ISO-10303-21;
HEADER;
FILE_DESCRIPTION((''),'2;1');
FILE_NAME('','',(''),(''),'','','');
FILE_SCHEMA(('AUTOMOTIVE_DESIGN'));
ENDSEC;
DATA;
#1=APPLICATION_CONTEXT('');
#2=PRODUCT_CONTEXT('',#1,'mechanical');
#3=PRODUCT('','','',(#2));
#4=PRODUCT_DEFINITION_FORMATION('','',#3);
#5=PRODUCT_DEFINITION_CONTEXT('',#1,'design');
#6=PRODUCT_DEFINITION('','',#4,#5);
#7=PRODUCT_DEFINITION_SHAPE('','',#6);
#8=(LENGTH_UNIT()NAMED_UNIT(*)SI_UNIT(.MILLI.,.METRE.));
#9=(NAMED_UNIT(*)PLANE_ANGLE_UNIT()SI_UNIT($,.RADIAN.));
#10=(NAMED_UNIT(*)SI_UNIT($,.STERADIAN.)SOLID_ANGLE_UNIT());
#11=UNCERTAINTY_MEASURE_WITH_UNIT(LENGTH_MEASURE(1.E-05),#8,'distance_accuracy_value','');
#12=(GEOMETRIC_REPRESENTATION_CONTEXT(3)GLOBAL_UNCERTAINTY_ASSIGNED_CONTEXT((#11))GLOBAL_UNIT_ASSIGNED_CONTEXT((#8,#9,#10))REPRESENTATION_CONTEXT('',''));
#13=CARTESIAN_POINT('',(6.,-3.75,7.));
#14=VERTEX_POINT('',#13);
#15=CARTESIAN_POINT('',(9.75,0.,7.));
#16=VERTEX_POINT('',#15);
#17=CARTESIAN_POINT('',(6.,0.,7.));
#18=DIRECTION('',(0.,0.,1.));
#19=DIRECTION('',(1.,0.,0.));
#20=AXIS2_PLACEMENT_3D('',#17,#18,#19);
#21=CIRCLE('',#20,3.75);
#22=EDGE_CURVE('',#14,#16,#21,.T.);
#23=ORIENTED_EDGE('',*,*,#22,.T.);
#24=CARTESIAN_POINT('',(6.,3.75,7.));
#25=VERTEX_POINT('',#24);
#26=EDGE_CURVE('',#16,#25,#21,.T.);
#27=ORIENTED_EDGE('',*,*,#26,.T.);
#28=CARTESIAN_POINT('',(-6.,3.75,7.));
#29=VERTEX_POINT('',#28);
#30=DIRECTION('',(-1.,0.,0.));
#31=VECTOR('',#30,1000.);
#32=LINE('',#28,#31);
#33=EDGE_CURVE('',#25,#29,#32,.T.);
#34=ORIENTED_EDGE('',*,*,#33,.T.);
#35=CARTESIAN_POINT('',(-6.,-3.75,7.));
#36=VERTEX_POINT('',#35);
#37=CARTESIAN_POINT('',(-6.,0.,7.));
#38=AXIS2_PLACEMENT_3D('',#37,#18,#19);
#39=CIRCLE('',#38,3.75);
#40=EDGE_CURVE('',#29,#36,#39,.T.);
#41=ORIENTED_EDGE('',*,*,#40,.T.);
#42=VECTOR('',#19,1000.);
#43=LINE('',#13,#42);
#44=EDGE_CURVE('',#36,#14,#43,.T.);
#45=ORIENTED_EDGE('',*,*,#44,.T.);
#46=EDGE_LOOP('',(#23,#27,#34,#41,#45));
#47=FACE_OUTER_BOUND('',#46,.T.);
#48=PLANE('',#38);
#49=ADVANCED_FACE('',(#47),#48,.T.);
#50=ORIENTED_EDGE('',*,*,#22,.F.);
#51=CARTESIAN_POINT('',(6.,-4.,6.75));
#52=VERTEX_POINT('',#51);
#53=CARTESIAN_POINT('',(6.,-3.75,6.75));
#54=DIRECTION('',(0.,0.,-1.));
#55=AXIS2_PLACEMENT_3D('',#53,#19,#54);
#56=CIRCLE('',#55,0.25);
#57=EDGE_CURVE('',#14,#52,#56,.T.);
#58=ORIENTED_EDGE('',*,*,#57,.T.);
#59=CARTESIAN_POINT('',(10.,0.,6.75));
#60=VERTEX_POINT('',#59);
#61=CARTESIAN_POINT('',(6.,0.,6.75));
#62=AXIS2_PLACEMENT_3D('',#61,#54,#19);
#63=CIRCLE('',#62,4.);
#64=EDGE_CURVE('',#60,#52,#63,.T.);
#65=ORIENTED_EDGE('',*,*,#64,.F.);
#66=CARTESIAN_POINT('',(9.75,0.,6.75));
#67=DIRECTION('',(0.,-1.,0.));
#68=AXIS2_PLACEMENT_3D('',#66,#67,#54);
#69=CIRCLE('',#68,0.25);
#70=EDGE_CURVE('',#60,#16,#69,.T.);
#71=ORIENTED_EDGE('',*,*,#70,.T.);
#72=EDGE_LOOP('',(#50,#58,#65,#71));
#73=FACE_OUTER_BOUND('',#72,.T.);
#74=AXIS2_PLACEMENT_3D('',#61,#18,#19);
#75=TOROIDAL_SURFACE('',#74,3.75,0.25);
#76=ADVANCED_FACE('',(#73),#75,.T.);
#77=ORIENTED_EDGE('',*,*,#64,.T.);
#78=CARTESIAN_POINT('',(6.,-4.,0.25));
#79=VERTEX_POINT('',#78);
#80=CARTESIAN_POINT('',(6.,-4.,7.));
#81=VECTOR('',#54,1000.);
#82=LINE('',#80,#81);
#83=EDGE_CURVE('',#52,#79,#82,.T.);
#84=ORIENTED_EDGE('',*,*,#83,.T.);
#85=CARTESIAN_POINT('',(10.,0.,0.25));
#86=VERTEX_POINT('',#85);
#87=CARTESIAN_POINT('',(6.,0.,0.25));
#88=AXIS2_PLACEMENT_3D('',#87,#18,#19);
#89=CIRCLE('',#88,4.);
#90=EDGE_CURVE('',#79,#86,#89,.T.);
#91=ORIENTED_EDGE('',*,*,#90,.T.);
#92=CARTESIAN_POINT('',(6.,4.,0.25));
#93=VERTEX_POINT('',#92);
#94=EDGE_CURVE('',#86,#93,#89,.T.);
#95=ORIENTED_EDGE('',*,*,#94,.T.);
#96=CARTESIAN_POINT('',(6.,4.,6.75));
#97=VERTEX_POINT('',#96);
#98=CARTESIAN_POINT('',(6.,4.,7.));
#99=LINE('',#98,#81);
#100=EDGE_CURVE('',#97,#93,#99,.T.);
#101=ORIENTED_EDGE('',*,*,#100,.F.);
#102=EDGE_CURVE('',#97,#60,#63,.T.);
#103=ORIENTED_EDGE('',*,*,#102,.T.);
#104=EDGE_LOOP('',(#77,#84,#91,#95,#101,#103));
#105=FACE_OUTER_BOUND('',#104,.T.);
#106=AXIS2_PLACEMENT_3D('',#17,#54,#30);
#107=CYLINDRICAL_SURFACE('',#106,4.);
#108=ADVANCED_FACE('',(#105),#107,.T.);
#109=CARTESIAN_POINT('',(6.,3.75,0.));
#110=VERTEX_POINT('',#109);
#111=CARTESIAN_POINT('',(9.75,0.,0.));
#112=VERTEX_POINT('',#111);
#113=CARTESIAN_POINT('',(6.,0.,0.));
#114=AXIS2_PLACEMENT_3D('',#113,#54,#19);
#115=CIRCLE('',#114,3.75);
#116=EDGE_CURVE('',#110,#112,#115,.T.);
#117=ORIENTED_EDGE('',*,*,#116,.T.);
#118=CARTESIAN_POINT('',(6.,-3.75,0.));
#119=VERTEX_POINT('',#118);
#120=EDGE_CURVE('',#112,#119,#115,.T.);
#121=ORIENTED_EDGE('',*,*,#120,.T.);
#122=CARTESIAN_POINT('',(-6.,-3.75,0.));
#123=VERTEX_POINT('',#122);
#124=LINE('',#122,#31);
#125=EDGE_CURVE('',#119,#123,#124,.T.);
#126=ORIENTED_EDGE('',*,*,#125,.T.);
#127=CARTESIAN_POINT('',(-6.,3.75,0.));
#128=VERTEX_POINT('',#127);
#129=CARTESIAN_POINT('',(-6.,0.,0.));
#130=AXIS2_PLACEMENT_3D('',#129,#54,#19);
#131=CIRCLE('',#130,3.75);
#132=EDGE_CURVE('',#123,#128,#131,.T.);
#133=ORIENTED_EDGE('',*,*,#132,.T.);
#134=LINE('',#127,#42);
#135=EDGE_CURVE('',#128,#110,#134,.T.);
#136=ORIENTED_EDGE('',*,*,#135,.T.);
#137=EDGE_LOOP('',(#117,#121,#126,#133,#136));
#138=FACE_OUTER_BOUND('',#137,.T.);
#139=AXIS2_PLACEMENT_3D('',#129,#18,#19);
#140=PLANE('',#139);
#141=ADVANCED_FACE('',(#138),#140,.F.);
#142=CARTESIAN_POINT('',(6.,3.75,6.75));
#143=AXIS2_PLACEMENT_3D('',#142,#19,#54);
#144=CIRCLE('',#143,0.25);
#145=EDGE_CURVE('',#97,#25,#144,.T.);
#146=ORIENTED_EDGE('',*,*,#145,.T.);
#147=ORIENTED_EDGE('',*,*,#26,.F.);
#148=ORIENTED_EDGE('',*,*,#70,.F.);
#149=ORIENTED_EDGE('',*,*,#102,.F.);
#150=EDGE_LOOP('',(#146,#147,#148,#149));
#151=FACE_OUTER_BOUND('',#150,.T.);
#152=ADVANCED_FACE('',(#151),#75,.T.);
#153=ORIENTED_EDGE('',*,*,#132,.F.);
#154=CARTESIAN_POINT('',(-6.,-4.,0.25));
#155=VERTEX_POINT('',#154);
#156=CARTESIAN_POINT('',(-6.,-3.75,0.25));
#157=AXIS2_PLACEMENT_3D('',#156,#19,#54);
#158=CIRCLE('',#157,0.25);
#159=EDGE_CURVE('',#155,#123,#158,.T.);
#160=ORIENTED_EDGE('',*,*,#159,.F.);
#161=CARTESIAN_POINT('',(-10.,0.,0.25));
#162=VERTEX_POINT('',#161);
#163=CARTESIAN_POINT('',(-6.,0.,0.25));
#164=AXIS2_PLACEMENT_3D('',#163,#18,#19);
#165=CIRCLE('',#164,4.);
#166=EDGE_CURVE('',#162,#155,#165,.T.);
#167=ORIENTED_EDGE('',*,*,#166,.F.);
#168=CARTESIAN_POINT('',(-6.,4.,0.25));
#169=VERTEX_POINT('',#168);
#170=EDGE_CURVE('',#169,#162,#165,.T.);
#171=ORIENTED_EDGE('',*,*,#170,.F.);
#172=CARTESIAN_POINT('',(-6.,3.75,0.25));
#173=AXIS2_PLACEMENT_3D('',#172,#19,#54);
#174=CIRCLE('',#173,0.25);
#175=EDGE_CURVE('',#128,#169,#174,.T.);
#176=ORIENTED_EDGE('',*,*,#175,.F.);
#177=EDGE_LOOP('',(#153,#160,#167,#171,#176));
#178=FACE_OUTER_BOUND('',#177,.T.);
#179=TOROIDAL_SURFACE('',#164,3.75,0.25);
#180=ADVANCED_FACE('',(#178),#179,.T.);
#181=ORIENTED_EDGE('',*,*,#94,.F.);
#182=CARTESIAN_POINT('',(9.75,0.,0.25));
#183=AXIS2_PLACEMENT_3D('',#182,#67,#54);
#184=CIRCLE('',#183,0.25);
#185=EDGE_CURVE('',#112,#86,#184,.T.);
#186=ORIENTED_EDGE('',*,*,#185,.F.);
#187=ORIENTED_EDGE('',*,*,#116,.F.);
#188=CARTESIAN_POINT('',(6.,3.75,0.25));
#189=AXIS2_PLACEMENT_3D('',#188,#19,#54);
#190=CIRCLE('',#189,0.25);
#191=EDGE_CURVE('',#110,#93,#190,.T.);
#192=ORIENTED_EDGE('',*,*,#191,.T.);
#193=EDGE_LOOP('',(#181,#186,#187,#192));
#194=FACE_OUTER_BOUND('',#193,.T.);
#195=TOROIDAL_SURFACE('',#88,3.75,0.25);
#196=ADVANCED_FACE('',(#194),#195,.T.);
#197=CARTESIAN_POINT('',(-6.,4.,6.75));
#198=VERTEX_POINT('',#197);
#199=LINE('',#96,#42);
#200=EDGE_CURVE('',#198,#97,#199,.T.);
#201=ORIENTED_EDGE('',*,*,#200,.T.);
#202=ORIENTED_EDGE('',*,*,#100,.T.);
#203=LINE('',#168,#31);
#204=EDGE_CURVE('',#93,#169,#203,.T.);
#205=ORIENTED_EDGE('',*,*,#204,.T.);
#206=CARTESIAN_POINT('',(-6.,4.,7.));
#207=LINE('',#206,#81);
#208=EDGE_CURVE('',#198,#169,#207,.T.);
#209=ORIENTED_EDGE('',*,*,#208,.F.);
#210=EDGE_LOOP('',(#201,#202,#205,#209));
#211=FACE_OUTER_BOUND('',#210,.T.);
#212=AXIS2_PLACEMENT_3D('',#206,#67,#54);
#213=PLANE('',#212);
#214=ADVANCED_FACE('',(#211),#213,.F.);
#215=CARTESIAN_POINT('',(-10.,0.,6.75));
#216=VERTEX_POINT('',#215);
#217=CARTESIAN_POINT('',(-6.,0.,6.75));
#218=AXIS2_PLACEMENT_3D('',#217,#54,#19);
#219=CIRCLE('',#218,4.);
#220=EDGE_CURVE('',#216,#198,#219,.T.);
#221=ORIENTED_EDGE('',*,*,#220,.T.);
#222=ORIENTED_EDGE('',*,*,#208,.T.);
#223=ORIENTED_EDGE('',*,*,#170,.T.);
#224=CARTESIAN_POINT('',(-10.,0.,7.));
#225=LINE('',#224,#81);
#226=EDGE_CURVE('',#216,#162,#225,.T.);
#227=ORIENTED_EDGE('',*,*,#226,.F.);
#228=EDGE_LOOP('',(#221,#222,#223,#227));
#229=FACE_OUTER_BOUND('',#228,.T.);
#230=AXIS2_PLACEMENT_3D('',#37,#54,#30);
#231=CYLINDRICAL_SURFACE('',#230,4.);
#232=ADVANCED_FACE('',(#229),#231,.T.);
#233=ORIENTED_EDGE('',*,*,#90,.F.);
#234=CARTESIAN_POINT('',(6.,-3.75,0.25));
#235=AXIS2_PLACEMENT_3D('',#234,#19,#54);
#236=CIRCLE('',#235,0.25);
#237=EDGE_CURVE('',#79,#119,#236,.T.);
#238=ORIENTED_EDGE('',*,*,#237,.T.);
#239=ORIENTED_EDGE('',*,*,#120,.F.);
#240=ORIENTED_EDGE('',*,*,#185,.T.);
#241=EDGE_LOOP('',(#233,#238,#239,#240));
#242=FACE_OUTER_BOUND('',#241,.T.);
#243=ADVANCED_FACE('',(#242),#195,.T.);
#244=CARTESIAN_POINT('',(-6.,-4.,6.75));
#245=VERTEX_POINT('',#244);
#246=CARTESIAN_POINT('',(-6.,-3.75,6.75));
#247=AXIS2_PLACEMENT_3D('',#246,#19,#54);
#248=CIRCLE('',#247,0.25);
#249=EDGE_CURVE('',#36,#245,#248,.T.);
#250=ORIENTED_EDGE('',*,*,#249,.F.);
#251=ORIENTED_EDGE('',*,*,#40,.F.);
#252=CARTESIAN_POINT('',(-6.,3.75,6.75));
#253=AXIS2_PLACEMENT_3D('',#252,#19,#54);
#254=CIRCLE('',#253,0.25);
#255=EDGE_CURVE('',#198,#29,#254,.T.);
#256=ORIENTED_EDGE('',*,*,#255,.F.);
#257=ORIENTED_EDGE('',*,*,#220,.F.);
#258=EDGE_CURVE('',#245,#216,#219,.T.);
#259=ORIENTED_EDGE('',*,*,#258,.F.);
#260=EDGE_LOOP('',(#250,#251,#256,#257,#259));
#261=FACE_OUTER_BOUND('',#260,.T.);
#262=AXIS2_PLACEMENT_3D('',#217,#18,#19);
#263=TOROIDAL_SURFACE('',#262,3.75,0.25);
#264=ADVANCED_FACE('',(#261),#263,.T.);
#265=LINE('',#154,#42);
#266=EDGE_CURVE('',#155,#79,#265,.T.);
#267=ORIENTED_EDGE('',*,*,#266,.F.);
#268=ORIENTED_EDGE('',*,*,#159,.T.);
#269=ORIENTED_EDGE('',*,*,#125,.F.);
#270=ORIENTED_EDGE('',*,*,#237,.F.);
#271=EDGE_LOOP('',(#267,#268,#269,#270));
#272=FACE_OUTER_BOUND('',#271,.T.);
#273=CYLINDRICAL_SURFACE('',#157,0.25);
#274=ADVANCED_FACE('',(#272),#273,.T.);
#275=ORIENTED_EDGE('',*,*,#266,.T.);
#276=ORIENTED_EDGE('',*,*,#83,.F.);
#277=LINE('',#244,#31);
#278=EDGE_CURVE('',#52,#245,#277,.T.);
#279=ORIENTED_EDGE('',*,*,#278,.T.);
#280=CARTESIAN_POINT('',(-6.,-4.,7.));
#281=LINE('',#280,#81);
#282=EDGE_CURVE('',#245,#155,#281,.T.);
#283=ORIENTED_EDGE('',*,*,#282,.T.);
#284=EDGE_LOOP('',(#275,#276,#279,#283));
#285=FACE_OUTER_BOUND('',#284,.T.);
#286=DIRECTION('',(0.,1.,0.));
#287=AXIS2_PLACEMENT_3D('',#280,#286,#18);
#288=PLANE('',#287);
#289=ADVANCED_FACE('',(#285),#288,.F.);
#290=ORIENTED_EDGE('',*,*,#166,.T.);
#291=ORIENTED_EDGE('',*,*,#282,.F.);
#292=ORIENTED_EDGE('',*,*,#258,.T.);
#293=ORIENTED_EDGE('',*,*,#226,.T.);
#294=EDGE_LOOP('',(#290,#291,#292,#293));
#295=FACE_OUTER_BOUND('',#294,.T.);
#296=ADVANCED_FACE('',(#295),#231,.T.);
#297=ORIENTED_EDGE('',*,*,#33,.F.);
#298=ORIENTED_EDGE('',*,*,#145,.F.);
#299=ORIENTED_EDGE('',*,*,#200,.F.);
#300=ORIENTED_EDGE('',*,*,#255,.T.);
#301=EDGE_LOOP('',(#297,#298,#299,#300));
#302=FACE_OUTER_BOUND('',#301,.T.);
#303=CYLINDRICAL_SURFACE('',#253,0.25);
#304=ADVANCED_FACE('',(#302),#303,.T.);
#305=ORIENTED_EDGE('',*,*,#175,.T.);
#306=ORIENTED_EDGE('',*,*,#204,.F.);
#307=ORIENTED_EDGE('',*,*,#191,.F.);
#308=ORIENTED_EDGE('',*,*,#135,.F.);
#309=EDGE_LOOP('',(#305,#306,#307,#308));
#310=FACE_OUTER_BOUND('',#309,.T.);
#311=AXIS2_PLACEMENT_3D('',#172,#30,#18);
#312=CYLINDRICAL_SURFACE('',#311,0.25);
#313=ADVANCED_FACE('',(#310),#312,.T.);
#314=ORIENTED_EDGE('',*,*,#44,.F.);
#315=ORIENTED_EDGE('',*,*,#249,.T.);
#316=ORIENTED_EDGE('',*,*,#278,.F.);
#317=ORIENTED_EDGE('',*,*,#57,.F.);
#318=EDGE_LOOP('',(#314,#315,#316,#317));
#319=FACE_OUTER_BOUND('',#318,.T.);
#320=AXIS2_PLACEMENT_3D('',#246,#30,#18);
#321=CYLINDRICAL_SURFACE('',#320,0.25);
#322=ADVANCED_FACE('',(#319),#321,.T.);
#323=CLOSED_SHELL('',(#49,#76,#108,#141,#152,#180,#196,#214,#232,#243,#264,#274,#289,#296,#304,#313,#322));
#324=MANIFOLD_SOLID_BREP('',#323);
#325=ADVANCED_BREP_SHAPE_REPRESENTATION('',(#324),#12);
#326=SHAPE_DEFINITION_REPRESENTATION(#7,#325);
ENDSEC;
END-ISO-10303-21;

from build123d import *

# Parameters (mm, degrees)
EXTRUDE_487_DEPTH = 7
FILLET_1_R        = 0.25


with BuildPart() as part:
    # 草图1 → Extrude 487 (new body)
    with BuildSketch(Plane.XY):
        with BuildLine():
            Line((-6, 4), (6, 4))
            ThreePointArc((6, 4), (10, 0), (6, -4))
            Line((6, -4), (-6, -4))
            ThreePointArc((-6, -4), (-10, 0), (-6, 4))
        make_face()
    extrude(amount=EXTRUDE_487_DEPTH)

    # 圆角1
    fillet_1_edges = [part.edges().sort_by_distance(p)[0] for p in [
        (10, 0, 7),
        (0, 4, 7),
        (-10, 0, 7),
        (0, 4, 0),
        (10, 0, 0),
        (0, -4, 0),
        (-10, 0, 0),
        (0, -4, 7),
    ]]
    fillet(fillet_1_edges, radius=FILLET_1_R)


solid = part.part
